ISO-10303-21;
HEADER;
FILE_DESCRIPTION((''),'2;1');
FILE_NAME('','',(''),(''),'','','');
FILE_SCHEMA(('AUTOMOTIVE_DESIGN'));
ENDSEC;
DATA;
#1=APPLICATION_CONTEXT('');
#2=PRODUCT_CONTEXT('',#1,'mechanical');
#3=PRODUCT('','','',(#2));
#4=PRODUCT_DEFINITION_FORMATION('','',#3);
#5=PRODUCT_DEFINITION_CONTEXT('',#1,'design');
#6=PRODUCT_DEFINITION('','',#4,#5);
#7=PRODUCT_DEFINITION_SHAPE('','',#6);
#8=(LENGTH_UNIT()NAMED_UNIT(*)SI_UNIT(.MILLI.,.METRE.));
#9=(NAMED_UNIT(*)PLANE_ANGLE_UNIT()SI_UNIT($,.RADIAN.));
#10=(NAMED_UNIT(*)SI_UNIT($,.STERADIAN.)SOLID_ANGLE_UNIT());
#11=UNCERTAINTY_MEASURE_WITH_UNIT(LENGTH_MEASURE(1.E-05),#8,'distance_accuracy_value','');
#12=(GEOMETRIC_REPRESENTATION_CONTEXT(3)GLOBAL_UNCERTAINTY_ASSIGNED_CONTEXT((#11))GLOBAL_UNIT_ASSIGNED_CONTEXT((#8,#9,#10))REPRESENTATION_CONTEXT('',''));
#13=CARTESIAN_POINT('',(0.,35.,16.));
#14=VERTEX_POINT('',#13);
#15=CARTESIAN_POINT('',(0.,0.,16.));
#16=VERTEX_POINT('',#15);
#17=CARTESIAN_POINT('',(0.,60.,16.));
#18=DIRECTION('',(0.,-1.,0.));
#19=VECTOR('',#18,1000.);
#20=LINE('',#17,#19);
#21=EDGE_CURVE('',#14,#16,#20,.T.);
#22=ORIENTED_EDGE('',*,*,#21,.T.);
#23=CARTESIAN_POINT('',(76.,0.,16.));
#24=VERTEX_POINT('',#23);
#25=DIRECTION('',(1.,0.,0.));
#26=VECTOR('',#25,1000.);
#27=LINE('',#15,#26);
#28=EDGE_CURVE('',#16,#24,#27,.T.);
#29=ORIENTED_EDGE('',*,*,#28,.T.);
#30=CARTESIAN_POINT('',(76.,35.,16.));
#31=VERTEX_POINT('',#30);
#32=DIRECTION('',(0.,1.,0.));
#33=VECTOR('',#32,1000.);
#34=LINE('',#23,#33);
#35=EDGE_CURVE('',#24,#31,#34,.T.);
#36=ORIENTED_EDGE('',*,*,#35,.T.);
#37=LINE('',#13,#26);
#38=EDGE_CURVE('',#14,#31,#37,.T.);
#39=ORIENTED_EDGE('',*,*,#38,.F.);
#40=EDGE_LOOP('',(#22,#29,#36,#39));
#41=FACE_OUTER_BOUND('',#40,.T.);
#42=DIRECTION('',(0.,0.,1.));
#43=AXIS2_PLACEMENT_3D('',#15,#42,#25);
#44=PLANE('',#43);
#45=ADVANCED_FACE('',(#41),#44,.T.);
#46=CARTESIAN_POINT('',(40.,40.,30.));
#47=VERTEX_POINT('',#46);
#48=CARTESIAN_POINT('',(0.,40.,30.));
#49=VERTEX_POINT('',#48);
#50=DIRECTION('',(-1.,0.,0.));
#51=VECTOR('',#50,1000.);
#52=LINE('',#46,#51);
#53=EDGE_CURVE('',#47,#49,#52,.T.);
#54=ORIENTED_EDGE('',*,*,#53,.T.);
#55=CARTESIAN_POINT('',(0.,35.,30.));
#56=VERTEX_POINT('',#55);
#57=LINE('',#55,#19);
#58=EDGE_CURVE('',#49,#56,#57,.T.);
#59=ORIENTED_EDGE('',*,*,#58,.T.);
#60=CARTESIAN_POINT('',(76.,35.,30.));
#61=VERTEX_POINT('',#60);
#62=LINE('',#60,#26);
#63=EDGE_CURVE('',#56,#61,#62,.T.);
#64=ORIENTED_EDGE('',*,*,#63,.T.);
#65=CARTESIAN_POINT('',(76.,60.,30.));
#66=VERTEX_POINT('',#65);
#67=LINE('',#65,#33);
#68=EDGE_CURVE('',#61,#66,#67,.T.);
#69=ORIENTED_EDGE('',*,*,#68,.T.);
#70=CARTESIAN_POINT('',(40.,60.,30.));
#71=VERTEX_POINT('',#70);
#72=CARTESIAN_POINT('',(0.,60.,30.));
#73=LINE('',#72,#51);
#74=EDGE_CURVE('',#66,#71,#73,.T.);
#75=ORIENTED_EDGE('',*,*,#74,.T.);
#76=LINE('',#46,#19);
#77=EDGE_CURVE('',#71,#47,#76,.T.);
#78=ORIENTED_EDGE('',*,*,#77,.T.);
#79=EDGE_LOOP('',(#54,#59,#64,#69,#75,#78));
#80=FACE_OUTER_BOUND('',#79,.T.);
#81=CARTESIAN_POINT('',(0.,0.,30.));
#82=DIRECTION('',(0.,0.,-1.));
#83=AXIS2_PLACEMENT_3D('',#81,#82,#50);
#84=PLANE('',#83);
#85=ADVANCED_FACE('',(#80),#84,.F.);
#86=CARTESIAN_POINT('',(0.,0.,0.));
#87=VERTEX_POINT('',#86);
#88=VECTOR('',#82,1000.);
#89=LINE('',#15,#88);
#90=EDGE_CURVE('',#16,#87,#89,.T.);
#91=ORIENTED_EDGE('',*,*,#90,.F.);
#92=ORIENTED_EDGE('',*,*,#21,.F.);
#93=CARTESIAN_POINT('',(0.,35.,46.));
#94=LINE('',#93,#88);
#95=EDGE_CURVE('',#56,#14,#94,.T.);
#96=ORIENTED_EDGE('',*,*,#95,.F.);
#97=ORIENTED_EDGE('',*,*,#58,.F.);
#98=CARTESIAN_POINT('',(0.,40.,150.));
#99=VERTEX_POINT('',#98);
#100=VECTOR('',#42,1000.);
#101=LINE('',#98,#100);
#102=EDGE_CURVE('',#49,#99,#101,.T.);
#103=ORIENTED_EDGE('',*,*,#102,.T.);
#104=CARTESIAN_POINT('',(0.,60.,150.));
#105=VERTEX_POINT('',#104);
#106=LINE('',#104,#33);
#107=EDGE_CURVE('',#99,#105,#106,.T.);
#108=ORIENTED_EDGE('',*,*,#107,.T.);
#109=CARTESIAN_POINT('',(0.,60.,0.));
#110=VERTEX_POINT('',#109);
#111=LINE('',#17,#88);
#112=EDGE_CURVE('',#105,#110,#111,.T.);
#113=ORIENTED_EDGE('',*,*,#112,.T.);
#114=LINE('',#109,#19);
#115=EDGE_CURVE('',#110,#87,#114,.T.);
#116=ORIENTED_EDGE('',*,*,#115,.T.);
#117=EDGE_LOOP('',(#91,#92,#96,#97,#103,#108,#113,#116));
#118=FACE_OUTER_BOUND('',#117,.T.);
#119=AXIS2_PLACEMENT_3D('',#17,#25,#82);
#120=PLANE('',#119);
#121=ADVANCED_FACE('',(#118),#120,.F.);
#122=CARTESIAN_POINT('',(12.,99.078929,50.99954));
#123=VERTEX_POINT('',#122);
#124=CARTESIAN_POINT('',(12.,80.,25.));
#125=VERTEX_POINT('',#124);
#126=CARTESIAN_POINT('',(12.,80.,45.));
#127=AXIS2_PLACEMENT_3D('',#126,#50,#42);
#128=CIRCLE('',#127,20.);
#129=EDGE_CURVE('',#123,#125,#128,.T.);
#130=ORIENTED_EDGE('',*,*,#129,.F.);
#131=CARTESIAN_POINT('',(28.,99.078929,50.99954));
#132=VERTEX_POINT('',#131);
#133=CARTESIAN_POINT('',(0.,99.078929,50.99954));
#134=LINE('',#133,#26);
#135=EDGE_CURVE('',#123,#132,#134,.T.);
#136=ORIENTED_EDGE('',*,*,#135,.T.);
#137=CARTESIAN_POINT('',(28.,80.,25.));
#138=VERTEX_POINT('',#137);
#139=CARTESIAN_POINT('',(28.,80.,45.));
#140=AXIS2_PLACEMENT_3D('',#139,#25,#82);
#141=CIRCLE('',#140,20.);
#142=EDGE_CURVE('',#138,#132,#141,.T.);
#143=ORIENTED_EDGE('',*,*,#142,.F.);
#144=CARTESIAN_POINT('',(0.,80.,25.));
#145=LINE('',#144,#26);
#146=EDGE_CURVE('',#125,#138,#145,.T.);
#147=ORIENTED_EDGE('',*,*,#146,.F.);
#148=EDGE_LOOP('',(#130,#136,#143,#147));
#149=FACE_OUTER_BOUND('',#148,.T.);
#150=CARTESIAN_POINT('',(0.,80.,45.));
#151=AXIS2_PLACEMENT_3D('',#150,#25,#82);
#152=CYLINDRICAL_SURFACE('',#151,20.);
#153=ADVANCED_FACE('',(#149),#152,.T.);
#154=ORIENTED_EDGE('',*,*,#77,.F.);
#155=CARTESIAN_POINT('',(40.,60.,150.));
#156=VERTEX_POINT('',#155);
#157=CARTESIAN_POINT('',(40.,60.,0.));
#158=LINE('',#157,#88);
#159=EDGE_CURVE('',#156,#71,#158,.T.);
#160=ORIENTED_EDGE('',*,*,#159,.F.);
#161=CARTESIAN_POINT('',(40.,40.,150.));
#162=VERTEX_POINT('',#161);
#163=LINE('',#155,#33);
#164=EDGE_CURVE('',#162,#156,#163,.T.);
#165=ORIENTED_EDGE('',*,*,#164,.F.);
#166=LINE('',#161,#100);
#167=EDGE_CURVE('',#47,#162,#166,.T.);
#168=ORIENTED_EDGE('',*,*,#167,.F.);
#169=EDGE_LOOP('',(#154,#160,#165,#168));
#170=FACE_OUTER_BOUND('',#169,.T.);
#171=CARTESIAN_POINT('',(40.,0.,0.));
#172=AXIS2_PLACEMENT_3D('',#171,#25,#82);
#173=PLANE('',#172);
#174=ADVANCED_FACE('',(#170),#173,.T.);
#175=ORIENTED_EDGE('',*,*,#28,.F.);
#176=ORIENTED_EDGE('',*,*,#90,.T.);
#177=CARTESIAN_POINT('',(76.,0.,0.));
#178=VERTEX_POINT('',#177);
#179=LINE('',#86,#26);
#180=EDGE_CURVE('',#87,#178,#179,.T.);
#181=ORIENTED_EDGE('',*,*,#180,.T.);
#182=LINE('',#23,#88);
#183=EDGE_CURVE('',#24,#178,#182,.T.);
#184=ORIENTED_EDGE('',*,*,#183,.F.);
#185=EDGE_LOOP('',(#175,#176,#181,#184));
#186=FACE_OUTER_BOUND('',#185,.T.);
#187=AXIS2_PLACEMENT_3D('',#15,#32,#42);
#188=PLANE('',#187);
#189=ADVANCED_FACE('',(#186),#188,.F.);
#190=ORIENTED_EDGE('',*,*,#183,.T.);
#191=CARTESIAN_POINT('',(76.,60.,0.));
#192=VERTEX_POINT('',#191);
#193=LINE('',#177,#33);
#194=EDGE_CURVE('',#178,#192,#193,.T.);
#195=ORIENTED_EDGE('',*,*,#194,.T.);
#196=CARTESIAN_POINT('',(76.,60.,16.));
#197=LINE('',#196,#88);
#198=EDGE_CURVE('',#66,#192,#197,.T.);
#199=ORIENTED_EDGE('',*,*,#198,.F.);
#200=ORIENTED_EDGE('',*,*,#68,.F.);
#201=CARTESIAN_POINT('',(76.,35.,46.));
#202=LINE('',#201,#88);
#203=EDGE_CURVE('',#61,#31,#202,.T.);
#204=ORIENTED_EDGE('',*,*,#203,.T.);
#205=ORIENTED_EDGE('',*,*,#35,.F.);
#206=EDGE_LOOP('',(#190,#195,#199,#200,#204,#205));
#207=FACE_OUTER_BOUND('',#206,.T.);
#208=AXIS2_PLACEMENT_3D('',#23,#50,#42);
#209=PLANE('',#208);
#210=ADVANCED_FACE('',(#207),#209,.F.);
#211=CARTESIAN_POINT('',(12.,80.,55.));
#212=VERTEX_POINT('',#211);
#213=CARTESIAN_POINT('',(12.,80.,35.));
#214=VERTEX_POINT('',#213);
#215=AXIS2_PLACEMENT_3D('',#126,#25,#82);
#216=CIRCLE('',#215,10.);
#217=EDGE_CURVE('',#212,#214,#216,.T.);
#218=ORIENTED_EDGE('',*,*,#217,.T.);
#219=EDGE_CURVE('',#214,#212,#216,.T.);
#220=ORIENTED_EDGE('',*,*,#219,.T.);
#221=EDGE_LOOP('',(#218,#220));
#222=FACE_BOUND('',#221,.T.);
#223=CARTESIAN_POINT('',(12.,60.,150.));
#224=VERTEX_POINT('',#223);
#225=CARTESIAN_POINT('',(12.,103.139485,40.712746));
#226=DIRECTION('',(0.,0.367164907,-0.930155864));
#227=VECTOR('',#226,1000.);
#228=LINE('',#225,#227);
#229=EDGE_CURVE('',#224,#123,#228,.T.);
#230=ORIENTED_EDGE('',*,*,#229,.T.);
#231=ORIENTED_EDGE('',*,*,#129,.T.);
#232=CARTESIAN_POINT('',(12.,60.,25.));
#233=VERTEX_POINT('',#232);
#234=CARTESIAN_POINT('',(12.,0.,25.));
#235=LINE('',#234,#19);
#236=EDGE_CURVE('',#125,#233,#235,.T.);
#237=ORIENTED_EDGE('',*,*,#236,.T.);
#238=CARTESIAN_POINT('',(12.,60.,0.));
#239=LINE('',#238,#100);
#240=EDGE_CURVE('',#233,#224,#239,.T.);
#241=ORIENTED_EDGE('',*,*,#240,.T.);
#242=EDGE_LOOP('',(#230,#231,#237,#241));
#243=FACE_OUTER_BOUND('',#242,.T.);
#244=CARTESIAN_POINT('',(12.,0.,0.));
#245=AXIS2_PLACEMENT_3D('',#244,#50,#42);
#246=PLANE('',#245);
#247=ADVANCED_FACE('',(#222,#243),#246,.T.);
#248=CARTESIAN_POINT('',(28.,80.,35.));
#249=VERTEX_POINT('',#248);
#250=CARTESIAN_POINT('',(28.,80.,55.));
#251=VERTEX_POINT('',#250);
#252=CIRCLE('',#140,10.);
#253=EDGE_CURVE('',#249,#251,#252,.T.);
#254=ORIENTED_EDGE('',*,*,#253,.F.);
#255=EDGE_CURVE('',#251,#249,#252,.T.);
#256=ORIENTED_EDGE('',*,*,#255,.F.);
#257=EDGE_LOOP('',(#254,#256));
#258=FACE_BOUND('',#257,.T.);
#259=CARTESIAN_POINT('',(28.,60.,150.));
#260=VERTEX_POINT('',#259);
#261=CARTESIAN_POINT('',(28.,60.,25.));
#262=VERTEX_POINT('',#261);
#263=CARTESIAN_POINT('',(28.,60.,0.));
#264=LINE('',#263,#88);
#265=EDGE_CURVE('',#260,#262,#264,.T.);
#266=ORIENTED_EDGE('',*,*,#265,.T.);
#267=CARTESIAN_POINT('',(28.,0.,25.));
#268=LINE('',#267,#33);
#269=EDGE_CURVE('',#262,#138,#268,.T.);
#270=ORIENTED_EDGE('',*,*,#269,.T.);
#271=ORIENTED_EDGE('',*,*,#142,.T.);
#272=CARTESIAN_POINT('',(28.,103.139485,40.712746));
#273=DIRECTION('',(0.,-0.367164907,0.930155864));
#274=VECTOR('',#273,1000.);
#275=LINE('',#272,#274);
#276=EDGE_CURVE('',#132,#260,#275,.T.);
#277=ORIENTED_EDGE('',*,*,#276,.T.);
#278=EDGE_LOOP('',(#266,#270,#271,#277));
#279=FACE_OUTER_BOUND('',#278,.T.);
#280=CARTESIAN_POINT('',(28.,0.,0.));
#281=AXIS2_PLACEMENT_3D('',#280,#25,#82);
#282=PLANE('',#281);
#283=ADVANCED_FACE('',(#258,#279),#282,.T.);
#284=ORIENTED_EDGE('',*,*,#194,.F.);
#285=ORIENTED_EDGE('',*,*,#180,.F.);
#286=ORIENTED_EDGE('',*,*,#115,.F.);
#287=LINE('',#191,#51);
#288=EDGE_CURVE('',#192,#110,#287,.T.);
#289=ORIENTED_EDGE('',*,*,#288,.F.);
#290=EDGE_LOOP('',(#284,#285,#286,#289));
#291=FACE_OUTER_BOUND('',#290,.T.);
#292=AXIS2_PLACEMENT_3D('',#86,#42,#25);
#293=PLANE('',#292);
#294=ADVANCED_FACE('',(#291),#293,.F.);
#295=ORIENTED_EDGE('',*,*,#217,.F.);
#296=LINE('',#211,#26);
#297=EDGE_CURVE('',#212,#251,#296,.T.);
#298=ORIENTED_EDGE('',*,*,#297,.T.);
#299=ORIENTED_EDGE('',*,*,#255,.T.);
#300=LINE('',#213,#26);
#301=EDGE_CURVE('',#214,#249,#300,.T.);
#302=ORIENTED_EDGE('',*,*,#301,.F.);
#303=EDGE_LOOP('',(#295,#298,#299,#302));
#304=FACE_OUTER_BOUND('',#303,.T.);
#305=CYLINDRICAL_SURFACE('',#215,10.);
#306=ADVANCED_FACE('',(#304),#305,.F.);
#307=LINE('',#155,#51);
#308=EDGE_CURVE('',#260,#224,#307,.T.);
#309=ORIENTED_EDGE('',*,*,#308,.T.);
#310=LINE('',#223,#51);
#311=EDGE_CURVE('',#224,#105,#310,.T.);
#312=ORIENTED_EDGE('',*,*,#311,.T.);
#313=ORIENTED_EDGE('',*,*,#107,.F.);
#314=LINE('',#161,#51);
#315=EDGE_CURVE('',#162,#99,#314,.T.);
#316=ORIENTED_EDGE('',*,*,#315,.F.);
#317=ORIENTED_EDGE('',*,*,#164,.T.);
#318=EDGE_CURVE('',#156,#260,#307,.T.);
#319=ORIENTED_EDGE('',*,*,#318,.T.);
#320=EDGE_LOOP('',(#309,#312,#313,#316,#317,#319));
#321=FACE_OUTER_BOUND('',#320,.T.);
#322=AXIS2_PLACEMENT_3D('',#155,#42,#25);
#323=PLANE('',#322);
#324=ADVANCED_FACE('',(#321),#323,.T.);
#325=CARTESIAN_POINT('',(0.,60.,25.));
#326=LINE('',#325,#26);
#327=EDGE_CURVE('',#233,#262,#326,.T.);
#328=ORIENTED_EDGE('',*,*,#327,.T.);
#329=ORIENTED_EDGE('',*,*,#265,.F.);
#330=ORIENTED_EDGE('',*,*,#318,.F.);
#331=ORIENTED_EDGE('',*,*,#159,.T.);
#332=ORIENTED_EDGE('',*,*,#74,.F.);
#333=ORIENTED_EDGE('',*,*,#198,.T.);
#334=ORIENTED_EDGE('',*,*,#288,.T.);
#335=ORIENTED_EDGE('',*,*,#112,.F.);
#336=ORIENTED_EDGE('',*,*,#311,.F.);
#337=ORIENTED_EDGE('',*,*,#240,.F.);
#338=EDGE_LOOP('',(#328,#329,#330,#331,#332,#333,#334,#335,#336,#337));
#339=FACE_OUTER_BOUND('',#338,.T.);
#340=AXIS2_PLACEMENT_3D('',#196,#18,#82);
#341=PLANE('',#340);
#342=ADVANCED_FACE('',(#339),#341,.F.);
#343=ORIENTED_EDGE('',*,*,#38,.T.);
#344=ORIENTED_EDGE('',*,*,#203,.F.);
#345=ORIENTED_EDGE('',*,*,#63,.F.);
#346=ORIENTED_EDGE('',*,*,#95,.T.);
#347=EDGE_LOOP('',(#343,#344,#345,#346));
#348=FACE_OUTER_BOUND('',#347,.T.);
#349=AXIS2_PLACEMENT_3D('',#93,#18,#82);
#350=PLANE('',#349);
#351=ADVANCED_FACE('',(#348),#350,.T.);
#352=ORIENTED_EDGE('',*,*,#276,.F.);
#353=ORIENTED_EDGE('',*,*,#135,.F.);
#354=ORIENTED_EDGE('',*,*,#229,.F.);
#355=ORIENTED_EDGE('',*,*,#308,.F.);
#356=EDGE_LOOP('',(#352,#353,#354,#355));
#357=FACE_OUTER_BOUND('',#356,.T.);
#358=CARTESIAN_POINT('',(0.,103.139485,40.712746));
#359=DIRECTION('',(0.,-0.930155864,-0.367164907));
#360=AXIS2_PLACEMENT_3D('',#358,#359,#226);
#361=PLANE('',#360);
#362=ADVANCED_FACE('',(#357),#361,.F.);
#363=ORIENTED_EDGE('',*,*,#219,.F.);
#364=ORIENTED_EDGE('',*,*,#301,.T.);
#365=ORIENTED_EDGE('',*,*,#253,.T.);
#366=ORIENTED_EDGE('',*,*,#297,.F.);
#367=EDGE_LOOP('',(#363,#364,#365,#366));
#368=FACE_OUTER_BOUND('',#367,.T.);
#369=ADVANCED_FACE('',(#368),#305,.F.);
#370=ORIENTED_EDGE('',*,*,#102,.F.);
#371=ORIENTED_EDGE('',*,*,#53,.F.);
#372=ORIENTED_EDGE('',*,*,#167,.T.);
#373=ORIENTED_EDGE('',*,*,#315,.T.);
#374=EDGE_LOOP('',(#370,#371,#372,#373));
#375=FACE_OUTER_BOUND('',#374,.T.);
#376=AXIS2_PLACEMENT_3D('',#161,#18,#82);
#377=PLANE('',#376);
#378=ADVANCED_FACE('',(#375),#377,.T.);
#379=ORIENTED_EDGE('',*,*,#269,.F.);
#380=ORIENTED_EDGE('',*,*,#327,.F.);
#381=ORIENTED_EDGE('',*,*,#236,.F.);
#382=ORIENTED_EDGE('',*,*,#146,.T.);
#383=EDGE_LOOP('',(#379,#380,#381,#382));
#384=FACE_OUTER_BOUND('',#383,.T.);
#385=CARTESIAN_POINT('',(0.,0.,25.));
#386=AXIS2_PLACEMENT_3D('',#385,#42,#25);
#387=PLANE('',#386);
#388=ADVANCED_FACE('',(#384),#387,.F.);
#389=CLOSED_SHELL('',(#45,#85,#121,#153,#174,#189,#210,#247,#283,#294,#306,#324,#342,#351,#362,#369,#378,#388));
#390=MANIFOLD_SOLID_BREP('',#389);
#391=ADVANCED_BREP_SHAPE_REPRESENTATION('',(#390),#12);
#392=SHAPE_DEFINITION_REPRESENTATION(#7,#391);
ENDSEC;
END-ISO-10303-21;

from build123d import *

# Parameters (mm, degrees)
BASE_PLATE_SKETCH_W    = 76
BASE_PLATE_SKETCH_H    = 60
BASE_PLATE_DEPTH       = 16
UPRIGHT_WALL_DEPTH     = 76
WALL_NOTCH_SKETCH_W    = 76
WALL_NOTCH_SKETCH_H    = 25
WALL_NOTCH_DEPTH       = 16
ARM_BLOCK_SKETCH_W     = 120
ARM_BLOCK_SKETCH_H     = 20
ARM_BLOCK_DEPTH        = 40
ARM_LUG_DEPTH          = 40
ARM_SIDE_CUT_A_DEPTH   = 12
ARM_START              = -12
ARM_SIDE_CUT_B_DEPTH   = 12
PIVOT_HOLE_20_SKETCH_R = 10
PIVOT_HOLE_20_DEPTH    = 16


with BuildPart() as part:
    # Base Plate Sketch → Base Plate (new body)
    with BuildSketch(Plane.XY):
        with Locations((38, 30)):
            Rectangle(BASE_PLATE_SKETCH_W, BASE_PLATE_SKETCH_H)
    extrude(amount=BASE_PLATE_DEPTH)

    # Upright Wall Sketch → Upright Wall (add)
    with BuildSketch(Plane(origin=(76, 0, 0), x_dir=(0, 0, -1), z_dir=(1, 0, 0))):
        Polygon((-16, 60), (-41, 60), (-46, 60), (-46, 35), (-16, 35), align=None)
    extrude(amount=-UPRIGHT_WALL_DEPTH)

    # Wall Notch Sketch → Wall Notch (cut)
    with BuildSketch(Plane.XY.offset(46)):
        with Locations((38, 47.5)):
            Rectangle(WALL_NOTCH_SKETCH_W, WALL_NOTCH_SKETCH_H)
    extrude(amount=-WALL_NOTCH_DEPTH, mode=Mode.SUBTRACT)

    # Arm Block Sketch → Arm Block (add)
    with BuildSketch(Plane.ZY):
        with Locations((90, 50)):
            Rectangle(ARM_BLOCK_SKETCH_W, ARM_BLOCK_SKETCH_H)
    extrude(amount=-ARM_BLOCK_DEPTH)

    # Arm Lug Sketch → Arm Lug (add)
    with BuildSketch(Plane(origin=(40, 0, 0), x_dir=(0, 0, -1), z_dir=(1, 0, 0))):
        with BuildLine():
            Line((-53.649750889, 98.032798162), (-150, 60))
            Line((-150, 60), (-30, 60))
            Line((-30, 60), (-25, 60))
            Line((-25, 60), (-25, 80))
            ThreePointArc((-25, 80), (-33.167646012, 96.124372828), (-50.99953991, 99.078928714))
            Line((-50.99953991, 99.078928714), (-53.649750889, 98.032798162))
        make_face()
    extrude(amount=-ARM_LUG_DEPTH)

    # Arm Side Cut A Sketch → Arm Side Cut A (cut)
    with BuildSketch(Plane(origin=(40, 0, 0), x_dir=(0, 0, -1), z_dir=(1, 0, 0))):
        with BuildLine():
            Line((-53.649750889, 98.032798162), (-150, 60))
            Line((-150, 60), (-30, 60))
            Line((-30, 60), (-25, 60))
            Line((-25, 60), (-25, 80))
            ThreePointArc((-25, 80), (-33.167646012, 96.124372828), (-50.99953991, 99.078928714))
            Line((-50.99953991, 99.078928714), (-53.649750889, 98.032798162))
        make_face()
    extrude(amount=-ARM_SIDE_CUT_A_DEPTH, mode=Mode.SUBTRACT)

    # Arm Side Cut B Sketch → Arm Side Cut B (cut)
    with BuildSketch(Plane.ZY.offset(ARM_START)):
        with BuildLine():
            Line((25, 80), (25, 60))
            Line((25, 60), (150, 60))
            Line((150, 60), (53.649750889, 98.032798162))
            Line((53.649750889, 98.032798162), (50.99953991, 99.078928714))
            ThreePointArc((50.99953991, 99.078928714), (33.167646012, 96.124372828), (25, 80))
        make_face()
    extrude(amount=ARM_SIDE_CUT_B_DEPTH, mode=Mode.SUBTRACT)

    # Pivot Hole Ø20 Sketch → Pivot Hole Ø20 (cut)
    with BuildSketch(Plane(origin=(28, 0, 0), x_dir=(0, 0, -1), z_dir=(1, 0, 0))):
        with Locations((-45, 80)):
            Circle(PIVOT_HOLE_20_SKETCH_R)
    extrude(amount=-PIVOT_HOLE_20_DEPTH, mode=Mode.SUBTRACT)


solid = part.part
